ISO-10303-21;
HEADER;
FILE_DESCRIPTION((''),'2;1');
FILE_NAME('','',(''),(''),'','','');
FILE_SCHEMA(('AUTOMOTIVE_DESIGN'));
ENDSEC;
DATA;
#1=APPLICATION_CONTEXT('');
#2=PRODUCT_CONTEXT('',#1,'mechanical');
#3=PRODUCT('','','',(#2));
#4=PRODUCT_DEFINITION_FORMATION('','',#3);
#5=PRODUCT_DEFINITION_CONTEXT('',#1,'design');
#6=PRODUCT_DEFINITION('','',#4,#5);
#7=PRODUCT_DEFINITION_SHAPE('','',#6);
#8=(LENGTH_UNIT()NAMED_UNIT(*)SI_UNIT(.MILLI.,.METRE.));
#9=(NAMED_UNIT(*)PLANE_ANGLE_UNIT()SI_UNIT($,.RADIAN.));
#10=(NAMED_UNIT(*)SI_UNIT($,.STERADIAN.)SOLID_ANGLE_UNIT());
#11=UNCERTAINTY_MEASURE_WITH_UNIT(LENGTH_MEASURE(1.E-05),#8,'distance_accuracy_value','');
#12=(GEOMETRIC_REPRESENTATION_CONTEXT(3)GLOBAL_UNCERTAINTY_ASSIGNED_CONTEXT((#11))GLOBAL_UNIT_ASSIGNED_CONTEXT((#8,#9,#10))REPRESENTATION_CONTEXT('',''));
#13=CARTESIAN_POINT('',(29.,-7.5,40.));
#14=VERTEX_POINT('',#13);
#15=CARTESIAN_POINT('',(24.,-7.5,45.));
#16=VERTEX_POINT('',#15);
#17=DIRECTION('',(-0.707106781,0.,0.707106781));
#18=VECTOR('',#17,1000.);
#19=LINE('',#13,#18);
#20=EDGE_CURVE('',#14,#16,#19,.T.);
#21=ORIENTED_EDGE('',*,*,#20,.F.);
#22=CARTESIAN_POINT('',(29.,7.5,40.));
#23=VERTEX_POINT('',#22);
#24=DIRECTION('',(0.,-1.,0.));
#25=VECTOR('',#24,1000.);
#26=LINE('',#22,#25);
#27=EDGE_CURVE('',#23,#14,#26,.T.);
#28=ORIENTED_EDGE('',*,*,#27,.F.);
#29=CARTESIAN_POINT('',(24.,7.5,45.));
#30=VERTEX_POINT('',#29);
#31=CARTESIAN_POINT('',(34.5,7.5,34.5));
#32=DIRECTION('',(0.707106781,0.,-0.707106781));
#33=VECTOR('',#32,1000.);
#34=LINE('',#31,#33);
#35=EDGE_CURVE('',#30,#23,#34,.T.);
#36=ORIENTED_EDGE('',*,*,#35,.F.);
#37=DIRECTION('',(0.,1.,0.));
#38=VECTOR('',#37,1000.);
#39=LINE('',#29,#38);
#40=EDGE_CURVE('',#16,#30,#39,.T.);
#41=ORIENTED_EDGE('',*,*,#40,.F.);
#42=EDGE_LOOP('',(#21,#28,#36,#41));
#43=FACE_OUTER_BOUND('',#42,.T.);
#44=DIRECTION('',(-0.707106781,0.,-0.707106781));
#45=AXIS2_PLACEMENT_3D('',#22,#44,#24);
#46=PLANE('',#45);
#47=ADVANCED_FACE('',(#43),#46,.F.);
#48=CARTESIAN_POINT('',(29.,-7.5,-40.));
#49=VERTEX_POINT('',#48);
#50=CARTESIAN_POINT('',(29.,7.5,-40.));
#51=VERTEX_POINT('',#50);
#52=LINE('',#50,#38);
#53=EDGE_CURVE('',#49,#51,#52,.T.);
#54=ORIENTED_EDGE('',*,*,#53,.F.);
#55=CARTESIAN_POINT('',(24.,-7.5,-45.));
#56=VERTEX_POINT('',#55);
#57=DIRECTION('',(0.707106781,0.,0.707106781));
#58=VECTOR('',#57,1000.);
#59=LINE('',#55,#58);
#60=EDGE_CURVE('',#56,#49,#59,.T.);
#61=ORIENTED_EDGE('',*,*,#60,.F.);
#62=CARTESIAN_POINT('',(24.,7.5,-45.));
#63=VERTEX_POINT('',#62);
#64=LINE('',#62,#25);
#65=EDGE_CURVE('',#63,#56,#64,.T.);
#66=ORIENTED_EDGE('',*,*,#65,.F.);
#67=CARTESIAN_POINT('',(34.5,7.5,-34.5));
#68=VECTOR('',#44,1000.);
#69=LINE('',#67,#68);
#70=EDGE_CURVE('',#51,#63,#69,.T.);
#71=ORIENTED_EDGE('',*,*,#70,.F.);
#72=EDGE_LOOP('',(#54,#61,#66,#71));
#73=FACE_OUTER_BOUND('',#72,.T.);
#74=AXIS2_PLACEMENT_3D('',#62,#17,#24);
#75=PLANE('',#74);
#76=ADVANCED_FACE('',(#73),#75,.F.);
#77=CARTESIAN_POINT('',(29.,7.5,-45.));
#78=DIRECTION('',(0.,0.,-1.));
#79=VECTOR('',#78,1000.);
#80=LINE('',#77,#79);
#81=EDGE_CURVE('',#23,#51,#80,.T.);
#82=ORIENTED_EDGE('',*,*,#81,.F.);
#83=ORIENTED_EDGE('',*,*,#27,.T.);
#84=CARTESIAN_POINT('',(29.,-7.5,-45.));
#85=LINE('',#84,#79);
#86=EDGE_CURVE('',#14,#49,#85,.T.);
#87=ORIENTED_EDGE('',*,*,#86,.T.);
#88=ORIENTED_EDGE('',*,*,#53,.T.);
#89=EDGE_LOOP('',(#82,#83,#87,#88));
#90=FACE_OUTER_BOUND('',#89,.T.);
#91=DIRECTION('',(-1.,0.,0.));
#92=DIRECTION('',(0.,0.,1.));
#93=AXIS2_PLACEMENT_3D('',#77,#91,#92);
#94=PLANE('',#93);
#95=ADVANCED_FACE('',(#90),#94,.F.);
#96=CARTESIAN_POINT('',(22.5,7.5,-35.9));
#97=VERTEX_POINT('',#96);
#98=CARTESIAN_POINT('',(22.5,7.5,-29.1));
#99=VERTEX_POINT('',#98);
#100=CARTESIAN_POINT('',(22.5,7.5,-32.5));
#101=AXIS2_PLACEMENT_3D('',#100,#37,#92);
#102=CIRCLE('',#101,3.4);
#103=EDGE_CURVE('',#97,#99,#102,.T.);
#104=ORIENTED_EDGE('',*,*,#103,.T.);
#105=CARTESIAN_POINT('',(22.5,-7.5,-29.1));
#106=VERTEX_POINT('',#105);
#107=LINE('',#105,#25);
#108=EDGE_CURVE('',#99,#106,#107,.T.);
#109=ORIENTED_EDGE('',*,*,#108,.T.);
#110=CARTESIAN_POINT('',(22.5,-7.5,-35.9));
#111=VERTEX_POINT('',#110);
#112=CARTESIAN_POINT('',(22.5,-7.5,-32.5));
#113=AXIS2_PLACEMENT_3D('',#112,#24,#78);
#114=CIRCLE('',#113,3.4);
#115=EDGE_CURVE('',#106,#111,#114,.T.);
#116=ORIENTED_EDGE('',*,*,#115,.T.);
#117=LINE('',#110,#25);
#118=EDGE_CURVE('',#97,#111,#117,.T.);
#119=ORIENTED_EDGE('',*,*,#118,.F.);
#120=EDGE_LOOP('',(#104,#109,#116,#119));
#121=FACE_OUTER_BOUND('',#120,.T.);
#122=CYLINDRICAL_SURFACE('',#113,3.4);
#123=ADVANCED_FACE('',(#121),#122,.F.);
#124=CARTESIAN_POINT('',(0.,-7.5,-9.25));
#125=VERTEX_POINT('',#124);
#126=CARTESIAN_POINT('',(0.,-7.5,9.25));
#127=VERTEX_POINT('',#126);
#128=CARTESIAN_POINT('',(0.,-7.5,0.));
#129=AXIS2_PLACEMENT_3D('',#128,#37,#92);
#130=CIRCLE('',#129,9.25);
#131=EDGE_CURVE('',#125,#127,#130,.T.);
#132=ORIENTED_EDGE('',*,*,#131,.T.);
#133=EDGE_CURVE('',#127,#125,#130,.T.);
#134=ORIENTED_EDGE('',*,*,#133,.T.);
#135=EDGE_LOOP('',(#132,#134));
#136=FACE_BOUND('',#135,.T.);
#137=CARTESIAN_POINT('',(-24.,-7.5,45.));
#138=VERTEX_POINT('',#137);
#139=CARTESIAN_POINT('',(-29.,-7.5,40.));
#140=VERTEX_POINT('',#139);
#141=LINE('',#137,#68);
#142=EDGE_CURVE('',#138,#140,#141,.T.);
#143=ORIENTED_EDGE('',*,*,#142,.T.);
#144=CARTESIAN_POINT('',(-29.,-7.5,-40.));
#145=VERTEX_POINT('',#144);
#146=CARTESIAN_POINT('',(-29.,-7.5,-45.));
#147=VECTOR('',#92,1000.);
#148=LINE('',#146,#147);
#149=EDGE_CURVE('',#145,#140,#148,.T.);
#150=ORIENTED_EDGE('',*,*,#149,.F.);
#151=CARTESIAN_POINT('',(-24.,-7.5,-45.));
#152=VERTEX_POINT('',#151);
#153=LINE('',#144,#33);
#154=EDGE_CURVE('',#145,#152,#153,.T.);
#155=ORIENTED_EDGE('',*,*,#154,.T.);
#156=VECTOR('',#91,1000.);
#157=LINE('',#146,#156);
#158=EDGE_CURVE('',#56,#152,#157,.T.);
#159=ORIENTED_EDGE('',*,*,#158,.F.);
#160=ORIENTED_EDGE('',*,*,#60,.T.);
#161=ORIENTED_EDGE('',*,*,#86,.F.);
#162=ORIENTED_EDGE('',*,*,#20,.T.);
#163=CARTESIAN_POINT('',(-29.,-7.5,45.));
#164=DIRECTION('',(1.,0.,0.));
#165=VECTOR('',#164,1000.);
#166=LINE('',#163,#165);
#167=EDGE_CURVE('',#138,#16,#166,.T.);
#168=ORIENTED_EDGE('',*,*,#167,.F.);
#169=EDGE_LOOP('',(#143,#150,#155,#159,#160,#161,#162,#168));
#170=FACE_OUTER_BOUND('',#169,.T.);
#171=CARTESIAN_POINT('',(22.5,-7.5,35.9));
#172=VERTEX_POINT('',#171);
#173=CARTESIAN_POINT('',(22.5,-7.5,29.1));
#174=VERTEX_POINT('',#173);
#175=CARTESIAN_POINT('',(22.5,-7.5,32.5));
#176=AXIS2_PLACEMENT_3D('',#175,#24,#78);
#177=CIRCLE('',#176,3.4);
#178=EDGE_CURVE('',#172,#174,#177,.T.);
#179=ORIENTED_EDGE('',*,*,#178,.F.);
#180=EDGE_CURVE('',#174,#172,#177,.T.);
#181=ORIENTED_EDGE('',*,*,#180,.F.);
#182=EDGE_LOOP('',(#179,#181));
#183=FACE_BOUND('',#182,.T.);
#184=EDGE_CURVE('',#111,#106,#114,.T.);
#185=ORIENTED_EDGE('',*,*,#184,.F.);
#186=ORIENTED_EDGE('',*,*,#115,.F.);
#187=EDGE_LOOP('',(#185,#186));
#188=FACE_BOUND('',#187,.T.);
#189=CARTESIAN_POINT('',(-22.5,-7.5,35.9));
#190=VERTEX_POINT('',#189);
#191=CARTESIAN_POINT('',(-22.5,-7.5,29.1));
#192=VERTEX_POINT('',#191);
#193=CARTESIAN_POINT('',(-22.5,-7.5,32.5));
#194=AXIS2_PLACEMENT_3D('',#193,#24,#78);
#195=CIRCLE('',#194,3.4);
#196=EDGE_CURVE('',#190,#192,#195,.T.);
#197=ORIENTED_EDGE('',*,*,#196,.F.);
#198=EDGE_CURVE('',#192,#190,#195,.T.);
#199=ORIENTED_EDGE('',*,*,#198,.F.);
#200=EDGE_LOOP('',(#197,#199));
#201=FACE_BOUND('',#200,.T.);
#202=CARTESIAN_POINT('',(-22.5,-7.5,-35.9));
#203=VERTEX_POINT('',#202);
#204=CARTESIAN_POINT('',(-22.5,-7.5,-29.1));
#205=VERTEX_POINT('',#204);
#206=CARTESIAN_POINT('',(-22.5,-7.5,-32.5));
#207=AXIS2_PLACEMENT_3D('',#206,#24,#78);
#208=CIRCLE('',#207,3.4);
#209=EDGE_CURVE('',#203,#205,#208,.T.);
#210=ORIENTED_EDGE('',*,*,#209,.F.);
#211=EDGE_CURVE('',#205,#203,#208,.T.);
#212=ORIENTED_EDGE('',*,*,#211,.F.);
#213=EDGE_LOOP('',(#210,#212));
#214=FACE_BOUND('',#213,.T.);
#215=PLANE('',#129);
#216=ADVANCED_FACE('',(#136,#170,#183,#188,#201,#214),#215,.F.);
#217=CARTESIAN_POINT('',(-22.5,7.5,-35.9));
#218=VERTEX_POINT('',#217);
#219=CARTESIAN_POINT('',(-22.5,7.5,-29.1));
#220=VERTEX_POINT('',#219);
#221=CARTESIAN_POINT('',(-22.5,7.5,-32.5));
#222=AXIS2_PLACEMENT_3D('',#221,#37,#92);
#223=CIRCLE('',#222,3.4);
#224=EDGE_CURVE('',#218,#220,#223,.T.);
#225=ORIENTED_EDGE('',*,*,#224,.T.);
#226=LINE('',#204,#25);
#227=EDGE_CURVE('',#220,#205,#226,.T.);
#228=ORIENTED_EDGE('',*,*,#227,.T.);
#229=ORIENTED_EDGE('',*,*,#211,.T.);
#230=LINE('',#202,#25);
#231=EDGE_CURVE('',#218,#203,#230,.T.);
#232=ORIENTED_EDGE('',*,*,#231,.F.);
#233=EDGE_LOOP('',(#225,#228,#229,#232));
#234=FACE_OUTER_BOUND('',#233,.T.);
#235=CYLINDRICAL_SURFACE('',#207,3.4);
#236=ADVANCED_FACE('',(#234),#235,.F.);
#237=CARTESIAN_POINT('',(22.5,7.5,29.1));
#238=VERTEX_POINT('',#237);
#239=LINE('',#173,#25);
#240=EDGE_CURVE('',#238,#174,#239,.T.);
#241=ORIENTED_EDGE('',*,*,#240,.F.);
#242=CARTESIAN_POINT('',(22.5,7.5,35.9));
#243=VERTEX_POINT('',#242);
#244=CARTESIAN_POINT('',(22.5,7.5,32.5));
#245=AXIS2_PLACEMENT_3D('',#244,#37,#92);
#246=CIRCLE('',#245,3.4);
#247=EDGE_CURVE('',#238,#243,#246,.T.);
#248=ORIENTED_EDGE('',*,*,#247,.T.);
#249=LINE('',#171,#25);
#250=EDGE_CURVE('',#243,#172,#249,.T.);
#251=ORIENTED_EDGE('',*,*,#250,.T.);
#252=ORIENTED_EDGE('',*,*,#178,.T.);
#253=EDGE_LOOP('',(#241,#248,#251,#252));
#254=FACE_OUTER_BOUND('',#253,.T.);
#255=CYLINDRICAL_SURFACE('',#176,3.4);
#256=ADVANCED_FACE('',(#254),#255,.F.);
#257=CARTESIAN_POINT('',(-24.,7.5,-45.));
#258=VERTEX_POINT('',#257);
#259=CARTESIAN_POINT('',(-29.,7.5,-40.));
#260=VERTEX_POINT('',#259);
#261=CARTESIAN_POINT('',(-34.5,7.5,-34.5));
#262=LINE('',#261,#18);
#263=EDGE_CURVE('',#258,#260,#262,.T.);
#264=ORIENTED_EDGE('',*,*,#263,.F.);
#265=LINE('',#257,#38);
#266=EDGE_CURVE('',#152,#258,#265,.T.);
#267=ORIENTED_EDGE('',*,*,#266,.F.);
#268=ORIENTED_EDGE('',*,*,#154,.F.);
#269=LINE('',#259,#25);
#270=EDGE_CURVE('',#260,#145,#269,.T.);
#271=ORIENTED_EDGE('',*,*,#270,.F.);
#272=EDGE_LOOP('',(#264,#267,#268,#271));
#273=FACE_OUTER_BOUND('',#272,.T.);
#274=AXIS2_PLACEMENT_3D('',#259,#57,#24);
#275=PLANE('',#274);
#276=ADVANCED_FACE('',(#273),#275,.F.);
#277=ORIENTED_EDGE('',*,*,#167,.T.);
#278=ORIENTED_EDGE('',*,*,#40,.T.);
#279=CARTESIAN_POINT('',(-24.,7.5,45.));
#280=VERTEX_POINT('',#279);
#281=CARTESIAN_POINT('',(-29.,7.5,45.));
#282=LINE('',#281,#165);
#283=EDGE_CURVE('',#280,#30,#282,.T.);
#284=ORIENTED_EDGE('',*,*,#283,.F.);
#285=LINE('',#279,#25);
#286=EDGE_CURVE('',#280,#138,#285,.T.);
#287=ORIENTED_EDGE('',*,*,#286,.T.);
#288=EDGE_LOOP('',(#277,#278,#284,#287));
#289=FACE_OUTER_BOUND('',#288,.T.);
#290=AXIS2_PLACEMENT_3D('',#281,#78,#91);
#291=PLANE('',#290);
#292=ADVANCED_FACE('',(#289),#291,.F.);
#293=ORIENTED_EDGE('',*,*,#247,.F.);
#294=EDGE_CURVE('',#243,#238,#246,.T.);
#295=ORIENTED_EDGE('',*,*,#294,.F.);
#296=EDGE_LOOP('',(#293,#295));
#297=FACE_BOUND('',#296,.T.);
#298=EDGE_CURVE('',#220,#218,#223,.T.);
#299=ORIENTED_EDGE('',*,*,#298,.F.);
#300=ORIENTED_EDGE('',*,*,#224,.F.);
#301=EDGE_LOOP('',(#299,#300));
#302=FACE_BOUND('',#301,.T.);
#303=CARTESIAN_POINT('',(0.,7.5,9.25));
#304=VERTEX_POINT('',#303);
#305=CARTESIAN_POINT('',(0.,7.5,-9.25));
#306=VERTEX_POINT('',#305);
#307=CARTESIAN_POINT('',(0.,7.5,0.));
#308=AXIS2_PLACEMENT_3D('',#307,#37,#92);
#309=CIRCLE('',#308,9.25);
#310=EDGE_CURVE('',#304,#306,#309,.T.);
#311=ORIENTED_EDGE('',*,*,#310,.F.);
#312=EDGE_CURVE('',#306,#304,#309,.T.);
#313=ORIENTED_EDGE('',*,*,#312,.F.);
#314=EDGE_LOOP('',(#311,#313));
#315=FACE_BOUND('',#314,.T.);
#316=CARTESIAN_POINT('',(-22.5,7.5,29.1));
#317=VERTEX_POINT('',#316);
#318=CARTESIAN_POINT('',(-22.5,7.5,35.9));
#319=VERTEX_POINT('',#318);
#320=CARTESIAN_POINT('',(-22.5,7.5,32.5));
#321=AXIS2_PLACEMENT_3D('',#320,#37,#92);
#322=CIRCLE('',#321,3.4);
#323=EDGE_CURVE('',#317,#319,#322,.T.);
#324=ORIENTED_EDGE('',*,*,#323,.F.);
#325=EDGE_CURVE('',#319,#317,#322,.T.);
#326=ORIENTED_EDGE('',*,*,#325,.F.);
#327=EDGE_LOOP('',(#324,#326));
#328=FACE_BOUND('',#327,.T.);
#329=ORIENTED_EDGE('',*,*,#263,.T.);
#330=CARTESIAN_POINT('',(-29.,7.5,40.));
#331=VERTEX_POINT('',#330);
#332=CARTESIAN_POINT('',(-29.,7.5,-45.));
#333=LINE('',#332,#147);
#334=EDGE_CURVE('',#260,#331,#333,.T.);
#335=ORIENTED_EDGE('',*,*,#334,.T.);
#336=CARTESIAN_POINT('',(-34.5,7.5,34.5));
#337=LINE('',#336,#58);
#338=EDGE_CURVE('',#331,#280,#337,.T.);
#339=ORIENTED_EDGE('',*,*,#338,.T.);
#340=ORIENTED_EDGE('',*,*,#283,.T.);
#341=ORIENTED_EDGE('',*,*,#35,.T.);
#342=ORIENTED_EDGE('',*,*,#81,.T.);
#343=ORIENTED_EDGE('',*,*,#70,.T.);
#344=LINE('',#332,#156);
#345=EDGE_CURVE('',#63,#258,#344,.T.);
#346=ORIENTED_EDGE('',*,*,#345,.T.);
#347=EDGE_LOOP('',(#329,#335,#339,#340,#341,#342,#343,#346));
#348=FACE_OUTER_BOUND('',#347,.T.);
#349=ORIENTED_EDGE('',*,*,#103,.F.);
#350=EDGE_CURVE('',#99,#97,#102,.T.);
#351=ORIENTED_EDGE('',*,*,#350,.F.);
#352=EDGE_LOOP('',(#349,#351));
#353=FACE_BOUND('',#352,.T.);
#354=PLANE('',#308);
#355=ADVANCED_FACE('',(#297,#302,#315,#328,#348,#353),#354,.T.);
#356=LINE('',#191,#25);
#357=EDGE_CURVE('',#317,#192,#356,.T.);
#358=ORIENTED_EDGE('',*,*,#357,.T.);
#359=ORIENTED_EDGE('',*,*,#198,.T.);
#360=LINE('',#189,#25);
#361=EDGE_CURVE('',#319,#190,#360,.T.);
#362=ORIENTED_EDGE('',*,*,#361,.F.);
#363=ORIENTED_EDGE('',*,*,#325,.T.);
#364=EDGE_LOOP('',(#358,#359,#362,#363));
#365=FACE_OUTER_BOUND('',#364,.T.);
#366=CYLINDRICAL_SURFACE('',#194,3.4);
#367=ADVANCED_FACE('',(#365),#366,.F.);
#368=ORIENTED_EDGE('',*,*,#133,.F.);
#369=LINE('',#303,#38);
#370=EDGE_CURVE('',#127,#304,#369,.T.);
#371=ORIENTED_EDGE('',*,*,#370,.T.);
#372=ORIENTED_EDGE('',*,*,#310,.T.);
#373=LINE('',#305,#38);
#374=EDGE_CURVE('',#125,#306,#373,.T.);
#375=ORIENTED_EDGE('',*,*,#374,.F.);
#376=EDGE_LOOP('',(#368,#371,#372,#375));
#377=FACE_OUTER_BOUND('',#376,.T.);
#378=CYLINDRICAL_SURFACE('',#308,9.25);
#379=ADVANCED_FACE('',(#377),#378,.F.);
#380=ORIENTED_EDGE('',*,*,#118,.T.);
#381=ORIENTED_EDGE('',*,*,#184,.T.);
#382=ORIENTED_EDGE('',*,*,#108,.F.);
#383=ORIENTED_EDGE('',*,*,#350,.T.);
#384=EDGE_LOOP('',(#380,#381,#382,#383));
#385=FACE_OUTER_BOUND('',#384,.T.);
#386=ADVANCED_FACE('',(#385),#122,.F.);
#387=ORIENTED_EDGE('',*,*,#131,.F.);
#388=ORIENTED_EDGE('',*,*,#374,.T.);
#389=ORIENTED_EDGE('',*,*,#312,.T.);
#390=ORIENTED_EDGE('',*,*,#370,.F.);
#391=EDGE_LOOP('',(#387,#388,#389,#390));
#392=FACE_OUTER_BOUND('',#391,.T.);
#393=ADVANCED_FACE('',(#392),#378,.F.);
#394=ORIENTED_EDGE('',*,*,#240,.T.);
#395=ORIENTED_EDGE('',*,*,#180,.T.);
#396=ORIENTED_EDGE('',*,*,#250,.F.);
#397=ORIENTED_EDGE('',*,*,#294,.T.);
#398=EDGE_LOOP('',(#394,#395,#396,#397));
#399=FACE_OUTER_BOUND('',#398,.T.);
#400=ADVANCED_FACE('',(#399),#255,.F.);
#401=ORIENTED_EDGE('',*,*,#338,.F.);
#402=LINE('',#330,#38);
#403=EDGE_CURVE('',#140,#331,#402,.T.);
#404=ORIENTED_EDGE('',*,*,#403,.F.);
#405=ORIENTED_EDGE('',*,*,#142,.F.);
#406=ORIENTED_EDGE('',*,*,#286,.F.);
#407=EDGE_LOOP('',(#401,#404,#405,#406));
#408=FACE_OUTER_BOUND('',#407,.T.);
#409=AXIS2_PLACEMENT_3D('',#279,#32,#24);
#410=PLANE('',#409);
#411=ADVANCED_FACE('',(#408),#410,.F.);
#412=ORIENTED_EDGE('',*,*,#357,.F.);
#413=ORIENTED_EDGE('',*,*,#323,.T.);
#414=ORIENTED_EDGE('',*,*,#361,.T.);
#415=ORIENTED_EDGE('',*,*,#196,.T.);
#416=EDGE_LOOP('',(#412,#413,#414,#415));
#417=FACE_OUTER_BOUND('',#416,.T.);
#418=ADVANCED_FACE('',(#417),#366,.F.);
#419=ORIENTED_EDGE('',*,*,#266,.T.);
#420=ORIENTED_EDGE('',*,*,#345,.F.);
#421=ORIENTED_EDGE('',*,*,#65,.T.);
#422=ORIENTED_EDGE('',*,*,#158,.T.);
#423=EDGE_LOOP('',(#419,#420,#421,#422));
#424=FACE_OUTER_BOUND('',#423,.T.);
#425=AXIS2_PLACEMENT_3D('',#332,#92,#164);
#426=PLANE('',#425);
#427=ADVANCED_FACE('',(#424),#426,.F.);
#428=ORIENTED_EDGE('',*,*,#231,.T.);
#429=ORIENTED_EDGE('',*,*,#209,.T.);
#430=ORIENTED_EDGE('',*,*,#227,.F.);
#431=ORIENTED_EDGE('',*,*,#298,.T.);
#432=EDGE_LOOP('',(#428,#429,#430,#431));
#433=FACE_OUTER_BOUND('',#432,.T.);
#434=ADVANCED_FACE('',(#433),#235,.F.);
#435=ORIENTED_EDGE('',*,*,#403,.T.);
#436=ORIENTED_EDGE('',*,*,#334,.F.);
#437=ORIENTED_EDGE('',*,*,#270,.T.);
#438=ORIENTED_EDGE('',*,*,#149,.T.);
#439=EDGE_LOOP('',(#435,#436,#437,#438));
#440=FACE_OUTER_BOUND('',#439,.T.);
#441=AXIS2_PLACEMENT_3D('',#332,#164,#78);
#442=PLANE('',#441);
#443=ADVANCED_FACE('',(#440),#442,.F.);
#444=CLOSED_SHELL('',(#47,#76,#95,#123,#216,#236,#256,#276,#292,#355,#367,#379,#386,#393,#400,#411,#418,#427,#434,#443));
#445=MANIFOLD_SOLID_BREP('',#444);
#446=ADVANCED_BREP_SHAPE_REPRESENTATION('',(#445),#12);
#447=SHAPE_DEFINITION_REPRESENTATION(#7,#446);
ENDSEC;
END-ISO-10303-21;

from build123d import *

# Parameters (mm, degrees)
SKETCH_1_W             = 58
SKETCH_1_H             = 90
EXTRUDE_1_DEPTH        = 7.5
HOLE_WIZARD_M8_1_D     = 6.8
HOLE_WIZARD_M8_1_DEPTH = 19.75
HOLE_WIZARD_M8_1_TIP   = 2.042926105
M20X1_5_1_D            = 18.5
M20X1_5_1_DEPTH        = 44.5
M20X1_5_1_TIP          = 5.557960726
CHAMFER_1_SIZE         = 5


with BuildPart() as part:
    # 草图1 → 凸台-拉伸1 (new, symmetric)
    with BuildSketch(Plane(origin=(0, 0, 0), x_dir=(1, 0, 0), z_dir=(0, 1, 0))):
        Rectangle(SKETCH_1_W, SKETCH_1_H)
    extrude(amount=EXTRUDE_1_DEPTH, both=True)

    # M8 螺纹孔1
    with Locations(Plane.XZ.offset(7.5)):
        with Locations((-22.5, -32.5), (22.5, -32.5), (22.5, 32.5), (-22.5, 32.5)):
            Hole(HOLE_WIZARD_M8_1_D / 2, depth=HOLE_WIZARD_M8_1_DEPTH)
            with Locations((0, 0, -(HOLE_WIZARD_M8_1_DEPTH + HOLE_WIZARD_M8_1_TIP / 2))):  # 118° drill point
                Cone(0, HOLE_WIZARD_M8_1_D / 2, HOLE_WIZARD_M8_1_TIP, mode=Mode.SUBTRACT)

    # M20x1.5 螺纹孔1
    with Locations(Plane(origin=(0, 7.5, 0), x_dir=(1, 0, 0), z_dir=(0, 1, 0))):
        with Locations((0, 0)):
            Hole(M20X1_5_1_D / 2, depth=M20X1_5_1_DEPTH)
            with Locations((0, 0, -(M20X1_5_1_DEPTH + M20X1_5_1_TIP / 2))):  # 118° drill point
                Cone(0, M20X1_5_1_D / 2, M20X1_5_1_TIP, mode=Mode.SUBTRACT)

    # 倒角1
    chamfer_1_edges = [part.edges().sort_by_distance(p)[0] for p in [
        (29, 0, 45),
        (-29, 0, 45),
        (-29, 0, -45),
        (29, 0, -45),
    ]]
    chamfer(chamfer_1_edges, length=CHAMFER_1_SIZE)


solid = part.part
